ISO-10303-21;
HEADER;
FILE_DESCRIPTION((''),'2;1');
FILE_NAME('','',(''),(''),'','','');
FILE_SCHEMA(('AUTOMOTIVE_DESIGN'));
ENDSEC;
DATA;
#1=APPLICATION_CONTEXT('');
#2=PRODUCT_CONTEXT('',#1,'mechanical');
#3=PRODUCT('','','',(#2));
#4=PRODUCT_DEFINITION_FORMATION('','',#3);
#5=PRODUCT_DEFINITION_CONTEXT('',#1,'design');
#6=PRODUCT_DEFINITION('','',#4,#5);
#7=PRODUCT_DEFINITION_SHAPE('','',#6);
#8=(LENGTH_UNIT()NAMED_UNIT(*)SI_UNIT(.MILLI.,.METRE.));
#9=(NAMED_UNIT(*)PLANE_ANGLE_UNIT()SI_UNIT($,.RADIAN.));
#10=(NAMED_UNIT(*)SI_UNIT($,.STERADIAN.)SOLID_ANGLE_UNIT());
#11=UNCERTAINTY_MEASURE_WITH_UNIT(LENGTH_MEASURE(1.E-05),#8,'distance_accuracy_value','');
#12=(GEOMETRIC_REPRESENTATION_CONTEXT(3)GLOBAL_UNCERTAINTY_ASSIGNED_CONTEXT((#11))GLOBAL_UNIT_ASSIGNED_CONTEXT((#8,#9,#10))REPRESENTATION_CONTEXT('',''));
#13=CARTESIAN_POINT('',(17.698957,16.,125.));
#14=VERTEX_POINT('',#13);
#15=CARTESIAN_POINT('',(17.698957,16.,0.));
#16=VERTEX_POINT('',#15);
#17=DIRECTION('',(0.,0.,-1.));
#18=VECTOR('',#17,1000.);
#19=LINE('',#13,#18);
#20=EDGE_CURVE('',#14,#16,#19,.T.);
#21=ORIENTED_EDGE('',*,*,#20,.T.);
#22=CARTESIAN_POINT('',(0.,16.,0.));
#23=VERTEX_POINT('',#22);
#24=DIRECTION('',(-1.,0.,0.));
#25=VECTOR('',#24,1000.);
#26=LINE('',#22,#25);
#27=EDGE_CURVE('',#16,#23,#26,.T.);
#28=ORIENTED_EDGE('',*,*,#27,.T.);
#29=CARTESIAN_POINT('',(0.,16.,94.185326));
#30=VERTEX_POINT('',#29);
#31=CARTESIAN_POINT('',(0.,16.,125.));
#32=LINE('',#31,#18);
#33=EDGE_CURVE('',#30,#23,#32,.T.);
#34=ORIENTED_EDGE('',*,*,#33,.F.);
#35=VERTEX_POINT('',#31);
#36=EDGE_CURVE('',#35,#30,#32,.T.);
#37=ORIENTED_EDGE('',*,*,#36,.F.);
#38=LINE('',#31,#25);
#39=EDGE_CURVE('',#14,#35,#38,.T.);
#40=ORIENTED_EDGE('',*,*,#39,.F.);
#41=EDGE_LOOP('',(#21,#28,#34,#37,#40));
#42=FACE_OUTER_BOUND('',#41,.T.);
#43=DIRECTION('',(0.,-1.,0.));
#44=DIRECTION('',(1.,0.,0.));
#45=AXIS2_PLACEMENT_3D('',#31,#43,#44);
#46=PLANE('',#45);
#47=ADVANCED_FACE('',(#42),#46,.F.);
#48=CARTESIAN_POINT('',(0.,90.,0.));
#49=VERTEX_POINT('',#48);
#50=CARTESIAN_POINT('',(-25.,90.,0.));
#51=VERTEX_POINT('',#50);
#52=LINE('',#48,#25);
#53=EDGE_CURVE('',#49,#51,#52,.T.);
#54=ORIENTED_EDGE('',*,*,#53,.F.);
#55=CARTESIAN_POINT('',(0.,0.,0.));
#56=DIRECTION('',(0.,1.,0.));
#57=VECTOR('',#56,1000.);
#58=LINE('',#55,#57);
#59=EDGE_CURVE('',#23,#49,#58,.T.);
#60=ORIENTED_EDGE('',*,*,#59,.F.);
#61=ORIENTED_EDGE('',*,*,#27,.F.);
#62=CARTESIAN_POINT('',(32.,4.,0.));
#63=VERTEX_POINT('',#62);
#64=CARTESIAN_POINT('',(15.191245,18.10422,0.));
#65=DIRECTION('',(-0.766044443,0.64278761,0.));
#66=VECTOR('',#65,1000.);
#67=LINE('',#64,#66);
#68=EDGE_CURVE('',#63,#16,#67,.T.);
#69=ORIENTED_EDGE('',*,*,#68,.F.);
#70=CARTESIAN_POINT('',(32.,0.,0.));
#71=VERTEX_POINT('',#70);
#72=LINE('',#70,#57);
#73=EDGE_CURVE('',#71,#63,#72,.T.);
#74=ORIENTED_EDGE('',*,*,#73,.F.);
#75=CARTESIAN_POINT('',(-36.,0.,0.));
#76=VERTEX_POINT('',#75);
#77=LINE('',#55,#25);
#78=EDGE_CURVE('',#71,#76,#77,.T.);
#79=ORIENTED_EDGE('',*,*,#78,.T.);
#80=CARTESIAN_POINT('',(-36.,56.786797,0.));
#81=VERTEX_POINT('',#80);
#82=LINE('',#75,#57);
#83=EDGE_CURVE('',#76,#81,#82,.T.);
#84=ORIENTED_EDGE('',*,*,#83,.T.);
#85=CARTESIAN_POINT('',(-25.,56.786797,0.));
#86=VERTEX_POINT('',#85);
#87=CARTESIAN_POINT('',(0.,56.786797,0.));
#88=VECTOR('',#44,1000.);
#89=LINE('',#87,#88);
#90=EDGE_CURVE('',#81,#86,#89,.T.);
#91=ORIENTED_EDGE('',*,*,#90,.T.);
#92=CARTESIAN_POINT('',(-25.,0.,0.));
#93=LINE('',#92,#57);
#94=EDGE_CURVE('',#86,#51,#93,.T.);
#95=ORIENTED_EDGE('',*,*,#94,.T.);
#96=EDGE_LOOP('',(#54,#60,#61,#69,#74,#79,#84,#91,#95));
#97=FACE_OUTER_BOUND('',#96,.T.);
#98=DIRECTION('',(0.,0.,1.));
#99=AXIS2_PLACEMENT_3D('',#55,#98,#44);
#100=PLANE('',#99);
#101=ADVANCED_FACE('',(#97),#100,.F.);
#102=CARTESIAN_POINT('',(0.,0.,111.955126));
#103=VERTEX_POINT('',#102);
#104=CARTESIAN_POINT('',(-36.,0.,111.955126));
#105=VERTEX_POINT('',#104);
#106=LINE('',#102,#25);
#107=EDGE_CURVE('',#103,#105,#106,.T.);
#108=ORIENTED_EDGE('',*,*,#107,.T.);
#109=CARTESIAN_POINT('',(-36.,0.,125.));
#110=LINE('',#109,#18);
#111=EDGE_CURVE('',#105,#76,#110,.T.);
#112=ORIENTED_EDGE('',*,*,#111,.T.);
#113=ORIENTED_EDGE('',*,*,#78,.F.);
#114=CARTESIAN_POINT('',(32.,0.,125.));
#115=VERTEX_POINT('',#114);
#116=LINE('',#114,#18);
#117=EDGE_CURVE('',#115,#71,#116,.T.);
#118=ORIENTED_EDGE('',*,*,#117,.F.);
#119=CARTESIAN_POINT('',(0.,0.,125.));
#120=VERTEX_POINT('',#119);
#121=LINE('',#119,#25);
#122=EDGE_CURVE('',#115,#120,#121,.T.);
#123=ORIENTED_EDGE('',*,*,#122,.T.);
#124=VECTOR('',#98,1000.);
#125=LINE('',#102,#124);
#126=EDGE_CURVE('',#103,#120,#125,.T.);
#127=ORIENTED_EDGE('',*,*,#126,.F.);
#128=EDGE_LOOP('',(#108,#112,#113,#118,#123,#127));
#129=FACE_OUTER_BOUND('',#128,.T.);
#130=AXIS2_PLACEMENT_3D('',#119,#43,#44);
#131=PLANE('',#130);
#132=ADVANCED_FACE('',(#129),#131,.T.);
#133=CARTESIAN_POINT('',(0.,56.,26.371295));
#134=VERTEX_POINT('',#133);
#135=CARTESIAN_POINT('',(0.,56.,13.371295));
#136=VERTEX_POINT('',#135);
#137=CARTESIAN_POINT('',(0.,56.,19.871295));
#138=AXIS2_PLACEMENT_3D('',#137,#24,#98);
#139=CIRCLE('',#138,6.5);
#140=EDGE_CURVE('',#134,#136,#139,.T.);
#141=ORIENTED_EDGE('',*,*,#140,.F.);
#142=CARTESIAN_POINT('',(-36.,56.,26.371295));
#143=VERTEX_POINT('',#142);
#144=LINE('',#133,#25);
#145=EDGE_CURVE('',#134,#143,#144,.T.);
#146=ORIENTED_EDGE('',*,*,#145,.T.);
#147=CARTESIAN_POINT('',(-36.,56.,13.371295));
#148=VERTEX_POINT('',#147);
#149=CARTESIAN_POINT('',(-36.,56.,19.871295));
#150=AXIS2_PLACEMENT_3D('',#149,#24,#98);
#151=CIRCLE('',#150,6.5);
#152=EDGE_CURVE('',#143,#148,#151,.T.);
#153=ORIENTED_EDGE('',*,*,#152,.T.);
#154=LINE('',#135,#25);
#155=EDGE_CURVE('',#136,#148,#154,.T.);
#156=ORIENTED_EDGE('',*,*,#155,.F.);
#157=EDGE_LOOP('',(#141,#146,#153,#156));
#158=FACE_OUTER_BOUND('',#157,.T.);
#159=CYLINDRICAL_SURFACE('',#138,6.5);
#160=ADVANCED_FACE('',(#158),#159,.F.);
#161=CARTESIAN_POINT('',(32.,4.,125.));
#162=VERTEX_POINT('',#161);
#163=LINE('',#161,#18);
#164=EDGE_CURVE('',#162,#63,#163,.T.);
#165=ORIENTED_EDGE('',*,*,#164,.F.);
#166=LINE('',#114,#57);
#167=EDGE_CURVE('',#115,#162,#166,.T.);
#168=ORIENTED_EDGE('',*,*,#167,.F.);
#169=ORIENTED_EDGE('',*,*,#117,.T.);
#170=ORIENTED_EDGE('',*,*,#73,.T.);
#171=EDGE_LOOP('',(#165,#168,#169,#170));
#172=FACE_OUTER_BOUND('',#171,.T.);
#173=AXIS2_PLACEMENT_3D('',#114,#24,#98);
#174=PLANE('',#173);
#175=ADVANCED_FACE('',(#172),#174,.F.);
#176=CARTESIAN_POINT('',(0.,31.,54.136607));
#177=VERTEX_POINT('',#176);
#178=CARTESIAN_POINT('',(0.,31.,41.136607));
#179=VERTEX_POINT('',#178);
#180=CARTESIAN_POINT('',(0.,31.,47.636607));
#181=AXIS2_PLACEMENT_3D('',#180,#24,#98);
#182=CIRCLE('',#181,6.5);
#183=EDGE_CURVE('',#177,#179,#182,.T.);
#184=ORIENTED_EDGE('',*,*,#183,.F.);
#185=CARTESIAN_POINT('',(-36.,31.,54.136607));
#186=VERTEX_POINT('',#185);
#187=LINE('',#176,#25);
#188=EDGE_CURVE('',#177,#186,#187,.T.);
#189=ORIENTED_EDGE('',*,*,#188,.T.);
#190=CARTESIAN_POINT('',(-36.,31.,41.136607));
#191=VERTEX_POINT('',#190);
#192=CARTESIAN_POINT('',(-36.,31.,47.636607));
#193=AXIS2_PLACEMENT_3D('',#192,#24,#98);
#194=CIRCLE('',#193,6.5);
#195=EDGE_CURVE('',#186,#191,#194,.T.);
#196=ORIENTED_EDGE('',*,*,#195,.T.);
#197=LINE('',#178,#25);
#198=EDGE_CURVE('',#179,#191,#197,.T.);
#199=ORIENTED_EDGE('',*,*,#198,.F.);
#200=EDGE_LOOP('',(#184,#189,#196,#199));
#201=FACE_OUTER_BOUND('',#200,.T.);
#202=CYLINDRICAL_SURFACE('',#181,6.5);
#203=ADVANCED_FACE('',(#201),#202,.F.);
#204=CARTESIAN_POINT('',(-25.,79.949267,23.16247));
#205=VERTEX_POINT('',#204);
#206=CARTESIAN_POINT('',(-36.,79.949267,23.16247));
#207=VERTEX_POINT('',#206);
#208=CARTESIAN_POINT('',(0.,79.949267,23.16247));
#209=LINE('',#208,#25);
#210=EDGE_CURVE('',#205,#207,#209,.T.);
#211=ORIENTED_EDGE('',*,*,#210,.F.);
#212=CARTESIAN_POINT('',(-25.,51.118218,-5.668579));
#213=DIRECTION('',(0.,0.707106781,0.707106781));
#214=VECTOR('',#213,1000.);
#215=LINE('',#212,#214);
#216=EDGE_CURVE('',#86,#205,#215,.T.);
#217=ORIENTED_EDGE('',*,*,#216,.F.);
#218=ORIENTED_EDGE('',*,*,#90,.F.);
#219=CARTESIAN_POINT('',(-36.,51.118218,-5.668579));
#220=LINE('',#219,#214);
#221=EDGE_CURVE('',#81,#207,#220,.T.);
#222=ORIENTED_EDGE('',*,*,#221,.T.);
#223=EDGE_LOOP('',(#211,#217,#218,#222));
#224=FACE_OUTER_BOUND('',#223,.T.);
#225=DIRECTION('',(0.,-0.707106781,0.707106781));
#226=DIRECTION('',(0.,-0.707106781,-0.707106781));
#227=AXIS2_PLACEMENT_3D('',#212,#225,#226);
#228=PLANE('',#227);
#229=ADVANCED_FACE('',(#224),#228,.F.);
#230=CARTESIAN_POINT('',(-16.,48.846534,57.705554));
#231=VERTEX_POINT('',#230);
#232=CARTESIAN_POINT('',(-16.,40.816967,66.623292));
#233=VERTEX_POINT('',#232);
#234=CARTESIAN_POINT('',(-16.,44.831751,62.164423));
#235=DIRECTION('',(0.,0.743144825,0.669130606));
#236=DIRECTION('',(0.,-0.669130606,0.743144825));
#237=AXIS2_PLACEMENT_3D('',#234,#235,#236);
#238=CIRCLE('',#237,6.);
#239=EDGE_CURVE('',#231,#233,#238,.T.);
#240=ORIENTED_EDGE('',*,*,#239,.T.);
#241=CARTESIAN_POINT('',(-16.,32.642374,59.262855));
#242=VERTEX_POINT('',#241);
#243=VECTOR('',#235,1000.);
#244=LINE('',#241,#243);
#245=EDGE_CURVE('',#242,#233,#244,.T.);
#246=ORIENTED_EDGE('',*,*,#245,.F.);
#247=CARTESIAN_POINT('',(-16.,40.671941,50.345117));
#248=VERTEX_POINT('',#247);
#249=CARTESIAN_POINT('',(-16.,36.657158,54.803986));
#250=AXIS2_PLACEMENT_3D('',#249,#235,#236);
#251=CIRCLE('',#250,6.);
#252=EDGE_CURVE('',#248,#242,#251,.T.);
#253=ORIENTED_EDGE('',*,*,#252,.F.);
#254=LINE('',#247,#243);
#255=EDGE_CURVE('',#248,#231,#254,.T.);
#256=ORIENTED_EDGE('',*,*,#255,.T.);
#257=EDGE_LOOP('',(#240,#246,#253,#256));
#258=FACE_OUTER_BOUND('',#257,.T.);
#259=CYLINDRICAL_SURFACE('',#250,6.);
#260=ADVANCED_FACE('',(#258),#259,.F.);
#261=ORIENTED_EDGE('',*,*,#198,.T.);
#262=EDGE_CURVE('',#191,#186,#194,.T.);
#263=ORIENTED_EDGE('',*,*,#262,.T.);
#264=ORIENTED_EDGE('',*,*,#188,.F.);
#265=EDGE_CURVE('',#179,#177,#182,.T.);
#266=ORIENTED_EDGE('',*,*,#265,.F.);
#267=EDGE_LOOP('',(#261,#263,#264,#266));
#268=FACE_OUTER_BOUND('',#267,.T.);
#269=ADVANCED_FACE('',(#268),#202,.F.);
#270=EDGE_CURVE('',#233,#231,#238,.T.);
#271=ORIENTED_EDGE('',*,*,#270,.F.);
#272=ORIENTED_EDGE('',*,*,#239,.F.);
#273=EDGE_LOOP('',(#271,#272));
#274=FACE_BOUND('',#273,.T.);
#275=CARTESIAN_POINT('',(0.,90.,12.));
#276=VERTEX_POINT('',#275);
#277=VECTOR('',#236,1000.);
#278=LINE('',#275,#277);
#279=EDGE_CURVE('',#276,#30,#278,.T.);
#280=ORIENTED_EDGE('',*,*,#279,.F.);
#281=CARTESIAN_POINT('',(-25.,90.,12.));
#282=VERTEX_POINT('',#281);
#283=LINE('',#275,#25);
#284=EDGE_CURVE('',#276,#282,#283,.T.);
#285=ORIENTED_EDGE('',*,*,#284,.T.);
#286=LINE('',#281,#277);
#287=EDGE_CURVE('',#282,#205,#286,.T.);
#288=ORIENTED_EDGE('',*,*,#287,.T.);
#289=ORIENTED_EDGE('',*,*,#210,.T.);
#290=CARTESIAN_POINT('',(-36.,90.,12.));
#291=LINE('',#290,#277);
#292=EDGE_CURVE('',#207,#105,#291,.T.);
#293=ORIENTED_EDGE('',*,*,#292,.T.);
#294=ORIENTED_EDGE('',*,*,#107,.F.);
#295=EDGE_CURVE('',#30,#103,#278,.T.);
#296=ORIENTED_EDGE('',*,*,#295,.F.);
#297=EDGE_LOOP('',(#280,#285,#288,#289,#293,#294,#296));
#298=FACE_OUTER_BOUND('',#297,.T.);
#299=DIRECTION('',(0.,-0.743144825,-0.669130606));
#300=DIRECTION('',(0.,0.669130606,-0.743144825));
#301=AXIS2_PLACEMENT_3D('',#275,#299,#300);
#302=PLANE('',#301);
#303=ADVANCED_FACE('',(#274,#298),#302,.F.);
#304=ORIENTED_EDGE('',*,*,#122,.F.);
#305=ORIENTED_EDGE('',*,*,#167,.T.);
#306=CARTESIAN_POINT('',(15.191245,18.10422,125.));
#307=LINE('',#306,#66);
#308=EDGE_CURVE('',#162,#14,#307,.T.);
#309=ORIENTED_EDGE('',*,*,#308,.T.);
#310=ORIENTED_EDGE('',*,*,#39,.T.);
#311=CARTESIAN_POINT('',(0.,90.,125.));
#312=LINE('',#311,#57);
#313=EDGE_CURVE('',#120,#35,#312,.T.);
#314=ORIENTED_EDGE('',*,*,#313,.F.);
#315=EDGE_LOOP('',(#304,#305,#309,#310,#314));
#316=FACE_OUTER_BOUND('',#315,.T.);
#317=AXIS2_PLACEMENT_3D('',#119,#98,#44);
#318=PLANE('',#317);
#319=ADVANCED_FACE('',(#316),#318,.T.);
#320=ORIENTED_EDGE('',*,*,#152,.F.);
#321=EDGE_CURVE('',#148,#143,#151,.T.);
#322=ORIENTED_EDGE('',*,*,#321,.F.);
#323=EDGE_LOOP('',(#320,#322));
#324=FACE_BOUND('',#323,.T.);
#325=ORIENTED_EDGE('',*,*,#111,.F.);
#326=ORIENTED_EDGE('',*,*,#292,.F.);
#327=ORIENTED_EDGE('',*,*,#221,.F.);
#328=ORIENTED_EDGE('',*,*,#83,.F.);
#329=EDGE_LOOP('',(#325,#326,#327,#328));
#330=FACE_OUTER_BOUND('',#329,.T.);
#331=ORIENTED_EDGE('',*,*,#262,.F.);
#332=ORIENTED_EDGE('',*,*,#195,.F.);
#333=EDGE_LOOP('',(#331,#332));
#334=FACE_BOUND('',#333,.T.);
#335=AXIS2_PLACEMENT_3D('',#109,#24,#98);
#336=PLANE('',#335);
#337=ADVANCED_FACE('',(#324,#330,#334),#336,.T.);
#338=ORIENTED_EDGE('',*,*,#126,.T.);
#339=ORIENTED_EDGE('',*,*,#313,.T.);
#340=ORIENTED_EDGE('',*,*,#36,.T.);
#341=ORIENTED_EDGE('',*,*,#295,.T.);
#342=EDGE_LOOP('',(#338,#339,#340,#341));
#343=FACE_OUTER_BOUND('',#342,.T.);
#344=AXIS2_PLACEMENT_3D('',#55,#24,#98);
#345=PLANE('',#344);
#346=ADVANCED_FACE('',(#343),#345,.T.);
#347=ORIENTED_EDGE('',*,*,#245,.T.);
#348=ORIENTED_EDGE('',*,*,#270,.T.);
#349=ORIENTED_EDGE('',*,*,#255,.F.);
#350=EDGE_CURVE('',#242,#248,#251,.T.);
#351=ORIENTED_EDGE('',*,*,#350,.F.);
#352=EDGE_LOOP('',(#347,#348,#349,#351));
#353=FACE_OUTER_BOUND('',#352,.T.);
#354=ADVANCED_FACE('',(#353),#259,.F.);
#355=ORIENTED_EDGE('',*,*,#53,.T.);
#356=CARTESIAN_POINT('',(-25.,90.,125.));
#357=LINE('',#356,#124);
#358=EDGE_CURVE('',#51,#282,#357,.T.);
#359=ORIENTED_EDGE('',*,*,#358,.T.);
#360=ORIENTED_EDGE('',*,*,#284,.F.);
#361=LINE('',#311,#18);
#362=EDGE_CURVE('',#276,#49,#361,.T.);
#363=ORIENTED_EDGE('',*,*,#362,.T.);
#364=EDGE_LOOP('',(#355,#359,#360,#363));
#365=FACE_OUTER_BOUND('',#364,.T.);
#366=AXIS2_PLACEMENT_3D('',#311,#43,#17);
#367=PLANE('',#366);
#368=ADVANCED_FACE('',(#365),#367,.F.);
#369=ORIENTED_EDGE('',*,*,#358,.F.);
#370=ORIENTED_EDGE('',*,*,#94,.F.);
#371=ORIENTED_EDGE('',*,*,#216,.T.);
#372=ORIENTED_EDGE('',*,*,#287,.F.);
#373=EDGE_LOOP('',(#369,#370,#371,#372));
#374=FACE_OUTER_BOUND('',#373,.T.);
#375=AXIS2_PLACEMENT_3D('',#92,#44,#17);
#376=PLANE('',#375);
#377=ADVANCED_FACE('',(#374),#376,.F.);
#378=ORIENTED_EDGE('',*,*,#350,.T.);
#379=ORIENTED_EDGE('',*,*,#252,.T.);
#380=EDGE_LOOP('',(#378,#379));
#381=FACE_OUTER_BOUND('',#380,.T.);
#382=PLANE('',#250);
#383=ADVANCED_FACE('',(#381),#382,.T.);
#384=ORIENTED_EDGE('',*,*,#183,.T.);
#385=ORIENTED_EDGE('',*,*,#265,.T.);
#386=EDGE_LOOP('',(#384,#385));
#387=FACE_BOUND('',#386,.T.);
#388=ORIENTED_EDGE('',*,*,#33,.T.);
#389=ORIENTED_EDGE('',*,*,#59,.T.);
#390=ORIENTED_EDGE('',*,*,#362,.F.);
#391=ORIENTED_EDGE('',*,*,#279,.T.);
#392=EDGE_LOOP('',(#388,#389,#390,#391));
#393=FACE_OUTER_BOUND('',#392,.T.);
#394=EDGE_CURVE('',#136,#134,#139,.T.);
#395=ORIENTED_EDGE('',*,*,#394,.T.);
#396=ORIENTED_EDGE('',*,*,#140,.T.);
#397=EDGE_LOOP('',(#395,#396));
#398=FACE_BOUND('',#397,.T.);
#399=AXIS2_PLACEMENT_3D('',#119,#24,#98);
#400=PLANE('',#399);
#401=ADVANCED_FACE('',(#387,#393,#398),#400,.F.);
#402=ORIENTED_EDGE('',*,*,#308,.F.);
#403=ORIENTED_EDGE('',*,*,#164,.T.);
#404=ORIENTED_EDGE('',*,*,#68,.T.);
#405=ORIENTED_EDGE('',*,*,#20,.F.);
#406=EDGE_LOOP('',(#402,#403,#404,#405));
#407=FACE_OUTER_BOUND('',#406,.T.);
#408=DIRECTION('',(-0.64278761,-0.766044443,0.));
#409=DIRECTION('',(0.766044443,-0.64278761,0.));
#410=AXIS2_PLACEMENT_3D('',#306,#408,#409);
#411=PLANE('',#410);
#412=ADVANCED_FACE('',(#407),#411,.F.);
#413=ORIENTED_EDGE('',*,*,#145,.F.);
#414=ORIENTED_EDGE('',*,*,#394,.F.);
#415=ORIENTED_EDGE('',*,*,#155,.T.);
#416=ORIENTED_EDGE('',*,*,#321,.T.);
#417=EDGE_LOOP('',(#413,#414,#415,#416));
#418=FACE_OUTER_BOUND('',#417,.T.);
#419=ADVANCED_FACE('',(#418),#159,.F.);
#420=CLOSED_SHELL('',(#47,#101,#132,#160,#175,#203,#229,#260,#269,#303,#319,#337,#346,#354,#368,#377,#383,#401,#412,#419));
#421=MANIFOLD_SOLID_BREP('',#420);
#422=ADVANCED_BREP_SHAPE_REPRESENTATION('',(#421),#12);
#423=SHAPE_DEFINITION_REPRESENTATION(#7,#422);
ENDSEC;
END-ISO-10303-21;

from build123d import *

# Parameters (mm, degrees)
BRACKET_BODY_DEPTH            = 125
PLATE_RELIEF_CUT_DEPTH        = 36
CROSS_HOLES_CUT_11_DEEP_DEPTH = 11
SKETCH3_4_R                   = 6.5
CROSS_HOLES_CUT_36_DEEP_DEPTH = 36
HOLE_12_SKETCH_R              = 6
HOLE_12_DEPTH                 = 11


with BuildPart() as part:
    # Bracket Profile Sketch → Bracket Body (new body)
    with BuildSketch(Plane.XY):
        Polygon((-36, 0), (0, 0), (0, 16), (0, 17.641196013), (0, 90), (-36, 90), align=None)
        Polygon((0, 0), (32, 0), (32, 4), (17.698956889, 16), (0, 16), align=None)
    extrude(amount=BRACKET_BODY_DEPTH)

    # Plate Relief Sketch → Plate Relief Cut (cut)
    with BuildSketch(Plane.ZY.offset(36)):
        Polygon((12, 90), (111.955126335, 0), (125, 0), (125, 90), align=None)
    extrude(amount=-PLATE_RELIEF_CUT_DEPTH, mode=Mode.SUBTRACT)

    # Cross Holes Sketch → Cross Holes Cut 11 Deep (cut)
    with BuildSketch(Plane.ZY.offset(36)):
        Polygon((-5.668578971, 51.118217594), (-13.477683521, 103.633494759), (27.976080454, 91.378914898), (26.142244571, 82.929041136), align=None)
    extrude(amount=-CROSS_HOLES_CUT_11_DEEP_DEPTH, mode=Mode.SUBTRACT)

    # Sketch3_4 → Cross Holes Cut 36 Deep (cut)
    with BuildSketch(Plane.ZY.offset(36)):
        with Locations((19.871294507, 56)):
            Circle(SKETCH3_4_R)
        with Locations((47.636607378, 31)):
            Circle(SKETCH3_4_R)
    extrude(amount=-CROSS_HOLES_CUT_36_DEEP_DEPTH, mode=Mode.SUBTRACT)

    # Hole _12 Sketch → Hole _12 (cut)
    with BuildSketch(Plane(origin=(0, 55.670912219, 50.126314512), x_dir=(1, 0, 0), z_dir=(0, 0.7431448254773981, 0.669130606358854))):
        with Locations(Location((-16, -16.198872821, 0), (0, 0, 270))):
            Circle(HOLE_12_SKETCH_R)
    extrude(amount=-HOLE_12_DEPTH, mode=Mode.SUBTRACT)


solid = part.part
